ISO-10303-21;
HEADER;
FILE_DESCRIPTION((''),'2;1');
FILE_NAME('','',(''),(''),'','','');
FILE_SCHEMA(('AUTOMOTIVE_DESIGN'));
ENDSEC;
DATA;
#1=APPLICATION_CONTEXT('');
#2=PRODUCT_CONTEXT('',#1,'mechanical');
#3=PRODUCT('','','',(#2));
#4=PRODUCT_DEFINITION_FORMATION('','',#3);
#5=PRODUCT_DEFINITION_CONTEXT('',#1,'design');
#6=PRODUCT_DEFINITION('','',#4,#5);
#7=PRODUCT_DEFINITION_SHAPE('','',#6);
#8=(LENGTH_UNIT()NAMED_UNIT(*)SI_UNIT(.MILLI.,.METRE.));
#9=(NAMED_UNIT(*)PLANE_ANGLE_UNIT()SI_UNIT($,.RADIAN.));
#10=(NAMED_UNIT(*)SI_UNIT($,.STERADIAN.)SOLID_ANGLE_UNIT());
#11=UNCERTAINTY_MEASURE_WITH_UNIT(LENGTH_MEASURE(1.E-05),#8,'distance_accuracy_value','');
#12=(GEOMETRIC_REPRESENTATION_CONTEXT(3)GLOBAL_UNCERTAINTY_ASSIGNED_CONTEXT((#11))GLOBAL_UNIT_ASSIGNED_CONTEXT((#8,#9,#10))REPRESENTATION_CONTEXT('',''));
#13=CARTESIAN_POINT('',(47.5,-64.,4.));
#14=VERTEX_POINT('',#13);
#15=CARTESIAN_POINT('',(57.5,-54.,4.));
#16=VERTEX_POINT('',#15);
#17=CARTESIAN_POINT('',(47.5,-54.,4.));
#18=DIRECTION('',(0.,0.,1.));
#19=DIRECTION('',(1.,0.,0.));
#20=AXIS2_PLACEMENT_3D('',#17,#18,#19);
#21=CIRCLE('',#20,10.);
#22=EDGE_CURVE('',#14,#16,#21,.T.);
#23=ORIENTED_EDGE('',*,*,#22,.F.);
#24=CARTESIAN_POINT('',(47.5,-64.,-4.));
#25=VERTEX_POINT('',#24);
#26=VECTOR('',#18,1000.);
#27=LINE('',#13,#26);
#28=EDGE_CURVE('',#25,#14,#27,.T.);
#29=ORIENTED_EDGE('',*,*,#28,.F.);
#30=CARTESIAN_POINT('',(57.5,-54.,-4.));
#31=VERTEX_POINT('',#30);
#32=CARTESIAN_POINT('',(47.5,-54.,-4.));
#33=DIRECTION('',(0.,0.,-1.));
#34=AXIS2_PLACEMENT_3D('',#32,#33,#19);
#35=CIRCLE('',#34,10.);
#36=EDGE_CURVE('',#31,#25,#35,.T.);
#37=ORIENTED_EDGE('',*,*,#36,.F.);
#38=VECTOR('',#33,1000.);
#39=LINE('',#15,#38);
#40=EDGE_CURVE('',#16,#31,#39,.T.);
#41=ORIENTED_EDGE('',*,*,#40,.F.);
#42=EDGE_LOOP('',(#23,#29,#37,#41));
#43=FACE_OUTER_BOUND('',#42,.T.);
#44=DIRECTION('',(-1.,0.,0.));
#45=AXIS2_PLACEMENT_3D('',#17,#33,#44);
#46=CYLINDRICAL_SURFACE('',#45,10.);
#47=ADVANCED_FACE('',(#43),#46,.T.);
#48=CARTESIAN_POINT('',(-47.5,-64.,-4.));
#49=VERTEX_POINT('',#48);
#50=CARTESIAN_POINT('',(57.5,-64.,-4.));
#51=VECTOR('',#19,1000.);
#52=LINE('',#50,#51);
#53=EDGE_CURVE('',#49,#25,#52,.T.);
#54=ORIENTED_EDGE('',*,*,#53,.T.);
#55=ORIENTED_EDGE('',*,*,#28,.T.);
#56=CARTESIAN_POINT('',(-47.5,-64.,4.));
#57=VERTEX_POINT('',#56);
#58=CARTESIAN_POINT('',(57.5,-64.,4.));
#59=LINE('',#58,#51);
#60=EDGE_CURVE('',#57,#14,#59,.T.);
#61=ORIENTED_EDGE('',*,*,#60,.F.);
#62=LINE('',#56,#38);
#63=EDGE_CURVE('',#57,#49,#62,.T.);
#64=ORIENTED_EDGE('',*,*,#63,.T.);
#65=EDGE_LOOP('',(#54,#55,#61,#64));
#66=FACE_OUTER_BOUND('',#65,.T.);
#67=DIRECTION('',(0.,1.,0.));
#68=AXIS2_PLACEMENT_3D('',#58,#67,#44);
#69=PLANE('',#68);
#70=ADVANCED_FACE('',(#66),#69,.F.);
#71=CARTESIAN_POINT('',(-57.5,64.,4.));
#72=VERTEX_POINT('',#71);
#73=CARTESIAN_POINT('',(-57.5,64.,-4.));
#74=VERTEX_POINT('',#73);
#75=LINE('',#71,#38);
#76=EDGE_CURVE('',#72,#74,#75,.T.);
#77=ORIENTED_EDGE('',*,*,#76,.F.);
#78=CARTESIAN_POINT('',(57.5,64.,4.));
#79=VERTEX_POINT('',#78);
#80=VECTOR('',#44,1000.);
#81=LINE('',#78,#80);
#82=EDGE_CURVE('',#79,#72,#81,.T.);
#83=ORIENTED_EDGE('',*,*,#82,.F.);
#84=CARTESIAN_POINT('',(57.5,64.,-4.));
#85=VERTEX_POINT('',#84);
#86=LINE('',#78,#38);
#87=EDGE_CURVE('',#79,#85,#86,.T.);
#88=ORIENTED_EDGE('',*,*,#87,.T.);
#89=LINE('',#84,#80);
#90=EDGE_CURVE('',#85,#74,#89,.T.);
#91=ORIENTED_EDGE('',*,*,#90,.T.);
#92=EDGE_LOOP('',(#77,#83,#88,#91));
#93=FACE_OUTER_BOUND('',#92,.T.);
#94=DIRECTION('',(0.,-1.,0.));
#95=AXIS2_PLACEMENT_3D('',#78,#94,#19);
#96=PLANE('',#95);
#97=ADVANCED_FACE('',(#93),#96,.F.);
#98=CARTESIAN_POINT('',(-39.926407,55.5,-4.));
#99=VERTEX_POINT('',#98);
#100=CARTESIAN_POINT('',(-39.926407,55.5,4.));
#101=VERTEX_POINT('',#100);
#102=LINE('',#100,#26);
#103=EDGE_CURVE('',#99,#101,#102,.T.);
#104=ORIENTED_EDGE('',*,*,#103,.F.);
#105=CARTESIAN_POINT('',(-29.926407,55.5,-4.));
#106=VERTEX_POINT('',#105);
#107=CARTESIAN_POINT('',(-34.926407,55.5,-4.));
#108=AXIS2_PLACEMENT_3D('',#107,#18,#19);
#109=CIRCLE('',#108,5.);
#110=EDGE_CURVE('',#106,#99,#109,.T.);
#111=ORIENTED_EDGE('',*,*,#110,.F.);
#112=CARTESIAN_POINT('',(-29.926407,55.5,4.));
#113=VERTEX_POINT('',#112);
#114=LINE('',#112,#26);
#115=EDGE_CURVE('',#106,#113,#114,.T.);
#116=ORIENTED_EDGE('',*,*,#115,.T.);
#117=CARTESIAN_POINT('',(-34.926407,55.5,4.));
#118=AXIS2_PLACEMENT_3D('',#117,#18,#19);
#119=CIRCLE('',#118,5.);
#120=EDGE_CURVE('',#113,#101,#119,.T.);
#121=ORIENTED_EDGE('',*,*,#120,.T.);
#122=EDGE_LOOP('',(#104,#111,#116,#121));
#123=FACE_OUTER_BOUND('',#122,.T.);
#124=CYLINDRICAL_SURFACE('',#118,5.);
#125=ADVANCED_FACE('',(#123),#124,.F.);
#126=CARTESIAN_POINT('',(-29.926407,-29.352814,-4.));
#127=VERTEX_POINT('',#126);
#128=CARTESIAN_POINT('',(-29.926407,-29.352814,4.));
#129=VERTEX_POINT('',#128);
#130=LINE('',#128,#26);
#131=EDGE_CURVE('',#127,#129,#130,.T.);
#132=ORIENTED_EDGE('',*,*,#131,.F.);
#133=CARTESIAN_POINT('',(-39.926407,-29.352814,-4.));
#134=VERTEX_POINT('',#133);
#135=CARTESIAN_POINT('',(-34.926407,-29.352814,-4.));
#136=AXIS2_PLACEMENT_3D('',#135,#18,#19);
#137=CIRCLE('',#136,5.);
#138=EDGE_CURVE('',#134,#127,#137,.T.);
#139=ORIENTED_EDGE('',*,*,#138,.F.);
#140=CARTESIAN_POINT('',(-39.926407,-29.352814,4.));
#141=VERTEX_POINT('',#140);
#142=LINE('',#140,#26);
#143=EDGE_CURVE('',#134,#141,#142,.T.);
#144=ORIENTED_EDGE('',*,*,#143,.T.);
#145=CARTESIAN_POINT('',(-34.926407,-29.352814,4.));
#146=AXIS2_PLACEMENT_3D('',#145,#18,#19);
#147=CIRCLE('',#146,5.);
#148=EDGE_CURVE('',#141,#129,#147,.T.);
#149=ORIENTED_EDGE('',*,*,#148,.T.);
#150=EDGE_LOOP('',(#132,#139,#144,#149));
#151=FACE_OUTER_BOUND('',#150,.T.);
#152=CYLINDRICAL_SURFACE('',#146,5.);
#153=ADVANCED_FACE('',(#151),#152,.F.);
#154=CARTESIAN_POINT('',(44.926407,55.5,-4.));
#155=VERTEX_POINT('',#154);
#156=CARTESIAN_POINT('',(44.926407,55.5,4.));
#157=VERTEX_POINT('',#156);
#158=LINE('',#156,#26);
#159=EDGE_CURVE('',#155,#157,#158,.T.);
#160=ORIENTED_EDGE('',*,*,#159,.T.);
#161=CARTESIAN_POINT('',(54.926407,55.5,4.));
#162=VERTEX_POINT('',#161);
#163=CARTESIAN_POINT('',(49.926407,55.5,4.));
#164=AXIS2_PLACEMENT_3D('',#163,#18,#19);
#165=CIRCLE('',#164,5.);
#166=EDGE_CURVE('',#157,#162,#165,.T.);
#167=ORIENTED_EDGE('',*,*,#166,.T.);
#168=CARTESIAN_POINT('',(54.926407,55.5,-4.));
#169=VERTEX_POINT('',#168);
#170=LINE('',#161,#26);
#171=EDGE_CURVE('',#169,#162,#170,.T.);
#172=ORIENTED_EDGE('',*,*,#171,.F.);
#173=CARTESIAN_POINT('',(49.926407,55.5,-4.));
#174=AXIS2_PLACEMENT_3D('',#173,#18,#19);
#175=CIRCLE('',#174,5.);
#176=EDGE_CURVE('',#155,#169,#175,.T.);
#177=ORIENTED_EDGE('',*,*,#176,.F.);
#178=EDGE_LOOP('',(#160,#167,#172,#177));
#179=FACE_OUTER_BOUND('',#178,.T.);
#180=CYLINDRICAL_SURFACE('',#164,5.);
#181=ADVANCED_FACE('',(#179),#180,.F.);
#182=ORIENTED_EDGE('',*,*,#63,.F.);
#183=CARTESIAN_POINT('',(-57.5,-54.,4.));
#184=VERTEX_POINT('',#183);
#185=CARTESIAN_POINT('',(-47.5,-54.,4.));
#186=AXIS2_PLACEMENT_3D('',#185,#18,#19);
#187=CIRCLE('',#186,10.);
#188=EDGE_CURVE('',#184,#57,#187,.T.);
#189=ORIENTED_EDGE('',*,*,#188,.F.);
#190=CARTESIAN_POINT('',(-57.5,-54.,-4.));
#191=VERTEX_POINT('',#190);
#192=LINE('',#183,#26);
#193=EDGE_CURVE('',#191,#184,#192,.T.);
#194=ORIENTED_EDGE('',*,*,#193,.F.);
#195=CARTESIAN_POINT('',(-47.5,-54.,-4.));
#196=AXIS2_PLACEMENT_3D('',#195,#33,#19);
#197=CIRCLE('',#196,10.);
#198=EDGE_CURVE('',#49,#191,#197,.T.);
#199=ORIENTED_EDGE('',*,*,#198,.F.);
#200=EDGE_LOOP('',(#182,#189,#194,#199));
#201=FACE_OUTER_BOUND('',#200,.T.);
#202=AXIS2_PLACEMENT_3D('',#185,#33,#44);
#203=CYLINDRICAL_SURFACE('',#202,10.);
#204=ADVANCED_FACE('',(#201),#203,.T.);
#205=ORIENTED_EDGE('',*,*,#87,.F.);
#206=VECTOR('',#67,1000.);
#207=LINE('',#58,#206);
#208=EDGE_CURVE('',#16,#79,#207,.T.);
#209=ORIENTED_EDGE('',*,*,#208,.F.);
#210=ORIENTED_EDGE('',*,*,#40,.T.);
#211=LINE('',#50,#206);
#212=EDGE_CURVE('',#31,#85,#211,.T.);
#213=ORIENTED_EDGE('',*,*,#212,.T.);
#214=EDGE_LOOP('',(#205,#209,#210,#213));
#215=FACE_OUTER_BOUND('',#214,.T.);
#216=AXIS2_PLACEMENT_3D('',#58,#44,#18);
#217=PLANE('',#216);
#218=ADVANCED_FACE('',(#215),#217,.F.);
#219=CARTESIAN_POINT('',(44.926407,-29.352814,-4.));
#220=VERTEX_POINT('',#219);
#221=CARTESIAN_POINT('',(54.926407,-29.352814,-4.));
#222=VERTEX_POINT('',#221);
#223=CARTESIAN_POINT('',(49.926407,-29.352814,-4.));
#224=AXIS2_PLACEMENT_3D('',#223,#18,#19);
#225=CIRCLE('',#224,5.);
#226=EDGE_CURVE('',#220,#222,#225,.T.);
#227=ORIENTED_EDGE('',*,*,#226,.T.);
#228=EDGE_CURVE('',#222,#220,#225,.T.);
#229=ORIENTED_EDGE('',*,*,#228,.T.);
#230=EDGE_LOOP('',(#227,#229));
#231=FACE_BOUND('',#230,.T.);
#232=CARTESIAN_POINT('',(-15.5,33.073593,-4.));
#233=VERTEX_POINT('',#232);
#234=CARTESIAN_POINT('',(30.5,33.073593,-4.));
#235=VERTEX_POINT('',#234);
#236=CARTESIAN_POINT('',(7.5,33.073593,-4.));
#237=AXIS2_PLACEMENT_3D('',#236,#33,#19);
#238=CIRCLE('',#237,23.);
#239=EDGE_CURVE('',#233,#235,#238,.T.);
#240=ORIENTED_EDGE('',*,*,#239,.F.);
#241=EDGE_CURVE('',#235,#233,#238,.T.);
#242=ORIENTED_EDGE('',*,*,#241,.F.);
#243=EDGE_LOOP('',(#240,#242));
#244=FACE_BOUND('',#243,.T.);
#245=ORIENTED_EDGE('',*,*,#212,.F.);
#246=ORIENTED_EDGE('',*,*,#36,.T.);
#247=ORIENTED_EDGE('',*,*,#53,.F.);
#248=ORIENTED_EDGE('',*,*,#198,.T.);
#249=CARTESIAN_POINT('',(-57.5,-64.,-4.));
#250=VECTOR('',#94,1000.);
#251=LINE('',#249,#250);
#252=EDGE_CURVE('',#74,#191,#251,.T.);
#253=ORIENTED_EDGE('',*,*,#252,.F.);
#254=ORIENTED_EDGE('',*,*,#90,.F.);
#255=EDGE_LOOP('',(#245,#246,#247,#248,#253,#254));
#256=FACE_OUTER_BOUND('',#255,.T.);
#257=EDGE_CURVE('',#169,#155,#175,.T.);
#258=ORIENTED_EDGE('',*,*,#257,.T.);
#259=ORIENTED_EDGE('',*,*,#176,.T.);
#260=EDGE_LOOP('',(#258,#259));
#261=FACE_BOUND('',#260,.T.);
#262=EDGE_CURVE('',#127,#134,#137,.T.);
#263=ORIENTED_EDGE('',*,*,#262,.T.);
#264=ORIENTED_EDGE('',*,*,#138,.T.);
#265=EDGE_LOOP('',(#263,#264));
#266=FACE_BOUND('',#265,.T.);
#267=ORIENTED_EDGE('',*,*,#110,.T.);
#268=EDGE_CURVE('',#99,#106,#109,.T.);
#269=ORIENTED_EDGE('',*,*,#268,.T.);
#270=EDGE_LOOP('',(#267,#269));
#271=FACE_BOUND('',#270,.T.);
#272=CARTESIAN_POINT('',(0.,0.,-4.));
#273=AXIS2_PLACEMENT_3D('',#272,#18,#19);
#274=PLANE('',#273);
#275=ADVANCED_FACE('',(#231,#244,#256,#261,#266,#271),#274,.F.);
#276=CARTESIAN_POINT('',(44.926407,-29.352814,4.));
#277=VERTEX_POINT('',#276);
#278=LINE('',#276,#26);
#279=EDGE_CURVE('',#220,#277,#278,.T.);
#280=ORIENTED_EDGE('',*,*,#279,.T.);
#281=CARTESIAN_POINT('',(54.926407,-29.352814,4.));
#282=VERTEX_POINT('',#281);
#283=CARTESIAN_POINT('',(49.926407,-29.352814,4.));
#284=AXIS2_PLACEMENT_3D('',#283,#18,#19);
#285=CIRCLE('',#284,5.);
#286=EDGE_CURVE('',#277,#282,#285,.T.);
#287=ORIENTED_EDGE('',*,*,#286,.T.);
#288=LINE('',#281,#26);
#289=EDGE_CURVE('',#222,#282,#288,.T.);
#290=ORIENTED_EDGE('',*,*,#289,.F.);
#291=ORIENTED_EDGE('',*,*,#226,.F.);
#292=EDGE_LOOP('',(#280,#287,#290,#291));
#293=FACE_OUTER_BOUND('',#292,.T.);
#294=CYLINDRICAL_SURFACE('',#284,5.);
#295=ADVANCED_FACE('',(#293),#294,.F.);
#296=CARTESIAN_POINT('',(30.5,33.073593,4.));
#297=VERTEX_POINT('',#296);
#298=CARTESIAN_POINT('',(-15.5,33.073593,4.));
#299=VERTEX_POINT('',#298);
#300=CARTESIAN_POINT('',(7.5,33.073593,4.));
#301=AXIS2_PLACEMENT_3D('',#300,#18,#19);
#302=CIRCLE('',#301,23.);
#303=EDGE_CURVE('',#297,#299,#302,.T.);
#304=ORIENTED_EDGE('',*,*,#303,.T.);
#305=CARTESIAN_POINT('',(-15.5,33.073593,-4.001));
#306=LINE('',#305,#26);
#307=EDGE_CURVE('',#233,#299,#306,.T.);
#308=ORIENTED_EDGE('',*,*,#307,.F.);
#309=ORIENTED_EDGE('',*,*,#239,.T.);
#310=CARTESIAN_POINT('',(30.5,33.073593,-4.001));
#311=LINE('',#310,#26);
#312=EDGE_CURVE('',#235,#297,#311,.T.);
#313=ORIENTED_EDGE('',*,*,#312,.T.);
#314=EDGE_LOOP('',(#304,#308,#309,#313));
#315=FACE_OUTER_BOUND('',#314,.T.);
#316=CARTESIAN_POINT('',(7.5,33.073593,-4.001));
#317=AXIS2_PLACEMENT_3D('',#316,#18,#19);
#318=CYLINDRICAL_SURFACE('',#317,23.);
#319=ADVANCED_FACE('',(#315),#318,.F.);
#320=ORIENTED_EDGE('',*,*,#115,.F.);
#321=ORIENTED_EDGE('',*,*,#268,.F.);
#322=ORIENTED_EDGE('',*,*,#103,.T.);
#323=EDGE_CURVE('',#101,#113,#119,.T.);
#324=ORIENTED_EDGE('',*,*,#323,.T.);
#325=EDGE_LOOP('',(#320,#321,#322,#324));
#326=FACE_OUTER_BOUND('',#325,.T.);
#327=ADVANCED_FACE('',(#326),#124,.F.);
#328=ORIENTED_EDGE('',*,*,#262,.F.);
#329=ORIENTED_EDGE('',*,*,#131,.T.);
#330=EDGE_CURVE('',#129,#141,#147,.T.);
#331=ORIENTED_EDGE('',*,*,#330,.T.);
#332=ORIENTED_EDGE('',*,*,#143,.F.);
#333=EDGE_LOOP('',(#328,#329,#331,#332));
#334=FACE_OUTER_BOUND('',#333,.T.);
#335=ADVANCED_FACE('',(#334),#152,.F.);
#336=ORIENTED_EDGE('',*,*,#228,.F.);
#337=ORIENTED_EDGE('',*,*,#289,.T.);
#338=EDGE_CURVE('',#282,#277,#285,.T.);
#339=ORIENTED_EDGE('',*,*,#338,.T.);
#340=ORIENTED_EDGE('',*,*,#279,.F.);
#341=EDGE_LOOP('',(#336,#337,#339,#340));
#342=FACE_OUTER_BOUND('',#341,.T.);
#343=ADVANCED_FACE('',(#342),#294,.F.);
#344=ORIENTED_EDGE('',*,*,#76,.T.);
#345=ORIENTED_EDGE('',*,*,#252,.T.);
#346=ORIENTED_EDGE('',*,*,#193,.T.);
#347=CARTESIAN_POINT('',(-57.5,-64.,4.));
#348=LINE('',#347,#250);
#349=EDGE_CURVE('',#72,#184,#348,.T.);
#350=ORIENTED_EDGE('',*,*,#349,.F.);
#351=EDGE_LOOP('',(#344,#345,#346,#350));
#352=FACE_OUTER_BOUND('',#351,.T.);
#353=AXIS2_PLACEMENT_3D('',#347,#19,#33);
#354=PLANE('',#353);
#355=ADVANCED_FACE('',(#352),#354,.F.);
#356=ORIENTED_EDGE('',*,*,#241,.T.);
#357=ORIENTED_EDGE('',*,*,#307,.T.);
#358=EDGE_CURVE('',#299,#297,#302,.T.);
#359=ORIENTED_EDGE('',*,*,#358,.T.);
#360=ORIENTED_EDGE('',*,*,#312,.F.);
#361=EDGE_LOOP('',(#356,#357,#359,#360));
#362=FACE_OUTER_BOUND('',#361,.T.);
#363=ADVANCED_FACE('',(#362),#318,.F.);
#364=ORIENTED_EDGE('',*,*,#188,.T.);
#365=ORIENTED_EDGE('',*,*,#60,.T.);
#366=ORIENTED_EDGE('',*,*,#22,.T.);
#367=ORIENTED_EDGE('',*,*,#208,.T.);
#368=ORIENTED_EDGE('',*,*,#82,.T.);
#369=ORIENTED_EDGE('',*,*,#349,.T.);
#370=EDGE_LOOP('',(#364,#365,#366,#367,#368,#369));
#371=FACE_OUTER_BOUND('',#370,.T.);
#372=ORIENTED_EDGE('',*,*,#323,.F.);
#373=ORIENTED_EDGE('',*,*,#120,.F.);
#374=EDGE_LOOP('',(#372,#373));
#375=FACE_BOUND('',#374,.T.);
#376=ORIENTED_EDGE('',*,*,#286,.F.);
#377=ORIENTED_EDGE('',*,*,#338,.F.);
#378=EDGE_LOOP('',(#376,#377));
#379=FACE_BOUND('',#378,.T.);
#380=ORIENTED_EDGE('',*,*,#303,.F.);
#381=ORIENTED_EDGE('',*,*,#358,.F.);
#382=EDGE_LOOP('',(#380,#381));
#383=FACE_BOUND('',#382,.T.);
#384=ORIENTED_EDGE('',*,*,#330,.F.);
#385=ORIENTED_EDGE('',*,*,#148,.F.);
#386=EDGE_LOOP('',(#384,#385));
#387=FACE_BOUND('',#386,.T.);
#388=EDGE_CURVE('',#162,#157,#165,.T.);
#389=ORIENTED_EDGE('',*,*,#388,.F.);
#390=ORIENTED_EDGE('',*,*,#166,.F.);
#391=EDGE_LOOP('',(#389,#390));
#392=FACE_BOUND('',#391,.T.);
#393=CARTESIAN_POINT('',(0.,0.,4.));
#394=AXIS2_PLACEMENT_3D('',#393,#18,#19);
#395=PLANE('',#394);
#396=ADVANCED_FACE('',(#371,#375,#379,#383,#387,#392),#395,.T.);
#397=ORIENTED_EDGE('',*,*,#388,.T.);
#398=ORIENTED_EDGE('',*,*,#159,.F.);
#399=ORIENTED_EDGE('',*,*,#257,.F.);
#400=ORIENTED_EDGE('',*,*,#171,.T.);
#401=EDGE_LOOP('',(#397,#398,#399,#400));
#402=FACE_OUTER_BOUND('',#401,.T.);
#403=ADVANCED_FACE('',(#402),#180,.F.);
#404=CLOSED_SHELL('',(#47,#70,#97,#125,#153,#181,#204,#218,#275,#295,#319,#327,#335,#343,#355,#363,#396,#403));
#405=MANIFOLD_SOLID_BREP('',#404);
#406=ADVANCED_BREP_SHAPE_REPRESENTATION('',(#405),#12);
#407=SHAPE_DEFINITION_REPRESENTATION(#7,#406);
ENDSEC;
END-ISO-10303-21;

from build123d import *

# Parameters (mm, degrees)
SKETCH1_W           = 115
SKETCH1_H           = 128
BOSS_EXTRUDE1_DEPTH = 4
F_10_HOLE1_D        = 10
FILLET1_R           = 10
CUT_EXTRUDE1_REACH  = 88.407
SKETCH4_R           = 23


with BuildPart() as part:
    # Sketch1 → Boss-Extrude1 (new, symmetric)
    with BuildSketch(Plane.XY):
        Rectangle(SKETCH1_W, SKETCH1_H)
    extrude(amount=BOSS_EXTRUDE1_DEPTH, both=True)

    # Ø10 Hole1 (through all)
    with Locations(Plane.XY.offset(4)):
        with Locations((-34.926406871, 55.5), (49.926406871, 55.5), (49.926406871, -29.352813742), (-34.926406871, -29.352813742)):
            Hole(F_10_HOLE1_D / 2)

    # Fillet1
    fillet1_edges = [part.edges().sort_by_distance(p)[0] for p in [
        (57.5, -64, 0),
        (-57.5, -64, 0),
    ]]
    fillet(fillet1_edges, radius=FILLET1_R)

    # Sketch4 → Cut-Extrude1 (cut, up to next)
    with BuildSketch(Plane.XY.offset(4), mode=Mode.PRIVATE) as cut_extrude1_sk1:
        with Locations((7.5, 33.073593129)):
            Circle(SKETCH4_R)
    cut_extrude1_tool1 = extrude(cut_extrude1_sk1.sketch, amount=-CUT_EXTRUDE1_REACH, mode=Mode.PRIVATE) & part.part
    add(cut_extrude1_tool1.solids().sort_by_distance((7.5, 33.073593, 4))[0], mode=Mode.SUBTRACT)


solid = part.part
